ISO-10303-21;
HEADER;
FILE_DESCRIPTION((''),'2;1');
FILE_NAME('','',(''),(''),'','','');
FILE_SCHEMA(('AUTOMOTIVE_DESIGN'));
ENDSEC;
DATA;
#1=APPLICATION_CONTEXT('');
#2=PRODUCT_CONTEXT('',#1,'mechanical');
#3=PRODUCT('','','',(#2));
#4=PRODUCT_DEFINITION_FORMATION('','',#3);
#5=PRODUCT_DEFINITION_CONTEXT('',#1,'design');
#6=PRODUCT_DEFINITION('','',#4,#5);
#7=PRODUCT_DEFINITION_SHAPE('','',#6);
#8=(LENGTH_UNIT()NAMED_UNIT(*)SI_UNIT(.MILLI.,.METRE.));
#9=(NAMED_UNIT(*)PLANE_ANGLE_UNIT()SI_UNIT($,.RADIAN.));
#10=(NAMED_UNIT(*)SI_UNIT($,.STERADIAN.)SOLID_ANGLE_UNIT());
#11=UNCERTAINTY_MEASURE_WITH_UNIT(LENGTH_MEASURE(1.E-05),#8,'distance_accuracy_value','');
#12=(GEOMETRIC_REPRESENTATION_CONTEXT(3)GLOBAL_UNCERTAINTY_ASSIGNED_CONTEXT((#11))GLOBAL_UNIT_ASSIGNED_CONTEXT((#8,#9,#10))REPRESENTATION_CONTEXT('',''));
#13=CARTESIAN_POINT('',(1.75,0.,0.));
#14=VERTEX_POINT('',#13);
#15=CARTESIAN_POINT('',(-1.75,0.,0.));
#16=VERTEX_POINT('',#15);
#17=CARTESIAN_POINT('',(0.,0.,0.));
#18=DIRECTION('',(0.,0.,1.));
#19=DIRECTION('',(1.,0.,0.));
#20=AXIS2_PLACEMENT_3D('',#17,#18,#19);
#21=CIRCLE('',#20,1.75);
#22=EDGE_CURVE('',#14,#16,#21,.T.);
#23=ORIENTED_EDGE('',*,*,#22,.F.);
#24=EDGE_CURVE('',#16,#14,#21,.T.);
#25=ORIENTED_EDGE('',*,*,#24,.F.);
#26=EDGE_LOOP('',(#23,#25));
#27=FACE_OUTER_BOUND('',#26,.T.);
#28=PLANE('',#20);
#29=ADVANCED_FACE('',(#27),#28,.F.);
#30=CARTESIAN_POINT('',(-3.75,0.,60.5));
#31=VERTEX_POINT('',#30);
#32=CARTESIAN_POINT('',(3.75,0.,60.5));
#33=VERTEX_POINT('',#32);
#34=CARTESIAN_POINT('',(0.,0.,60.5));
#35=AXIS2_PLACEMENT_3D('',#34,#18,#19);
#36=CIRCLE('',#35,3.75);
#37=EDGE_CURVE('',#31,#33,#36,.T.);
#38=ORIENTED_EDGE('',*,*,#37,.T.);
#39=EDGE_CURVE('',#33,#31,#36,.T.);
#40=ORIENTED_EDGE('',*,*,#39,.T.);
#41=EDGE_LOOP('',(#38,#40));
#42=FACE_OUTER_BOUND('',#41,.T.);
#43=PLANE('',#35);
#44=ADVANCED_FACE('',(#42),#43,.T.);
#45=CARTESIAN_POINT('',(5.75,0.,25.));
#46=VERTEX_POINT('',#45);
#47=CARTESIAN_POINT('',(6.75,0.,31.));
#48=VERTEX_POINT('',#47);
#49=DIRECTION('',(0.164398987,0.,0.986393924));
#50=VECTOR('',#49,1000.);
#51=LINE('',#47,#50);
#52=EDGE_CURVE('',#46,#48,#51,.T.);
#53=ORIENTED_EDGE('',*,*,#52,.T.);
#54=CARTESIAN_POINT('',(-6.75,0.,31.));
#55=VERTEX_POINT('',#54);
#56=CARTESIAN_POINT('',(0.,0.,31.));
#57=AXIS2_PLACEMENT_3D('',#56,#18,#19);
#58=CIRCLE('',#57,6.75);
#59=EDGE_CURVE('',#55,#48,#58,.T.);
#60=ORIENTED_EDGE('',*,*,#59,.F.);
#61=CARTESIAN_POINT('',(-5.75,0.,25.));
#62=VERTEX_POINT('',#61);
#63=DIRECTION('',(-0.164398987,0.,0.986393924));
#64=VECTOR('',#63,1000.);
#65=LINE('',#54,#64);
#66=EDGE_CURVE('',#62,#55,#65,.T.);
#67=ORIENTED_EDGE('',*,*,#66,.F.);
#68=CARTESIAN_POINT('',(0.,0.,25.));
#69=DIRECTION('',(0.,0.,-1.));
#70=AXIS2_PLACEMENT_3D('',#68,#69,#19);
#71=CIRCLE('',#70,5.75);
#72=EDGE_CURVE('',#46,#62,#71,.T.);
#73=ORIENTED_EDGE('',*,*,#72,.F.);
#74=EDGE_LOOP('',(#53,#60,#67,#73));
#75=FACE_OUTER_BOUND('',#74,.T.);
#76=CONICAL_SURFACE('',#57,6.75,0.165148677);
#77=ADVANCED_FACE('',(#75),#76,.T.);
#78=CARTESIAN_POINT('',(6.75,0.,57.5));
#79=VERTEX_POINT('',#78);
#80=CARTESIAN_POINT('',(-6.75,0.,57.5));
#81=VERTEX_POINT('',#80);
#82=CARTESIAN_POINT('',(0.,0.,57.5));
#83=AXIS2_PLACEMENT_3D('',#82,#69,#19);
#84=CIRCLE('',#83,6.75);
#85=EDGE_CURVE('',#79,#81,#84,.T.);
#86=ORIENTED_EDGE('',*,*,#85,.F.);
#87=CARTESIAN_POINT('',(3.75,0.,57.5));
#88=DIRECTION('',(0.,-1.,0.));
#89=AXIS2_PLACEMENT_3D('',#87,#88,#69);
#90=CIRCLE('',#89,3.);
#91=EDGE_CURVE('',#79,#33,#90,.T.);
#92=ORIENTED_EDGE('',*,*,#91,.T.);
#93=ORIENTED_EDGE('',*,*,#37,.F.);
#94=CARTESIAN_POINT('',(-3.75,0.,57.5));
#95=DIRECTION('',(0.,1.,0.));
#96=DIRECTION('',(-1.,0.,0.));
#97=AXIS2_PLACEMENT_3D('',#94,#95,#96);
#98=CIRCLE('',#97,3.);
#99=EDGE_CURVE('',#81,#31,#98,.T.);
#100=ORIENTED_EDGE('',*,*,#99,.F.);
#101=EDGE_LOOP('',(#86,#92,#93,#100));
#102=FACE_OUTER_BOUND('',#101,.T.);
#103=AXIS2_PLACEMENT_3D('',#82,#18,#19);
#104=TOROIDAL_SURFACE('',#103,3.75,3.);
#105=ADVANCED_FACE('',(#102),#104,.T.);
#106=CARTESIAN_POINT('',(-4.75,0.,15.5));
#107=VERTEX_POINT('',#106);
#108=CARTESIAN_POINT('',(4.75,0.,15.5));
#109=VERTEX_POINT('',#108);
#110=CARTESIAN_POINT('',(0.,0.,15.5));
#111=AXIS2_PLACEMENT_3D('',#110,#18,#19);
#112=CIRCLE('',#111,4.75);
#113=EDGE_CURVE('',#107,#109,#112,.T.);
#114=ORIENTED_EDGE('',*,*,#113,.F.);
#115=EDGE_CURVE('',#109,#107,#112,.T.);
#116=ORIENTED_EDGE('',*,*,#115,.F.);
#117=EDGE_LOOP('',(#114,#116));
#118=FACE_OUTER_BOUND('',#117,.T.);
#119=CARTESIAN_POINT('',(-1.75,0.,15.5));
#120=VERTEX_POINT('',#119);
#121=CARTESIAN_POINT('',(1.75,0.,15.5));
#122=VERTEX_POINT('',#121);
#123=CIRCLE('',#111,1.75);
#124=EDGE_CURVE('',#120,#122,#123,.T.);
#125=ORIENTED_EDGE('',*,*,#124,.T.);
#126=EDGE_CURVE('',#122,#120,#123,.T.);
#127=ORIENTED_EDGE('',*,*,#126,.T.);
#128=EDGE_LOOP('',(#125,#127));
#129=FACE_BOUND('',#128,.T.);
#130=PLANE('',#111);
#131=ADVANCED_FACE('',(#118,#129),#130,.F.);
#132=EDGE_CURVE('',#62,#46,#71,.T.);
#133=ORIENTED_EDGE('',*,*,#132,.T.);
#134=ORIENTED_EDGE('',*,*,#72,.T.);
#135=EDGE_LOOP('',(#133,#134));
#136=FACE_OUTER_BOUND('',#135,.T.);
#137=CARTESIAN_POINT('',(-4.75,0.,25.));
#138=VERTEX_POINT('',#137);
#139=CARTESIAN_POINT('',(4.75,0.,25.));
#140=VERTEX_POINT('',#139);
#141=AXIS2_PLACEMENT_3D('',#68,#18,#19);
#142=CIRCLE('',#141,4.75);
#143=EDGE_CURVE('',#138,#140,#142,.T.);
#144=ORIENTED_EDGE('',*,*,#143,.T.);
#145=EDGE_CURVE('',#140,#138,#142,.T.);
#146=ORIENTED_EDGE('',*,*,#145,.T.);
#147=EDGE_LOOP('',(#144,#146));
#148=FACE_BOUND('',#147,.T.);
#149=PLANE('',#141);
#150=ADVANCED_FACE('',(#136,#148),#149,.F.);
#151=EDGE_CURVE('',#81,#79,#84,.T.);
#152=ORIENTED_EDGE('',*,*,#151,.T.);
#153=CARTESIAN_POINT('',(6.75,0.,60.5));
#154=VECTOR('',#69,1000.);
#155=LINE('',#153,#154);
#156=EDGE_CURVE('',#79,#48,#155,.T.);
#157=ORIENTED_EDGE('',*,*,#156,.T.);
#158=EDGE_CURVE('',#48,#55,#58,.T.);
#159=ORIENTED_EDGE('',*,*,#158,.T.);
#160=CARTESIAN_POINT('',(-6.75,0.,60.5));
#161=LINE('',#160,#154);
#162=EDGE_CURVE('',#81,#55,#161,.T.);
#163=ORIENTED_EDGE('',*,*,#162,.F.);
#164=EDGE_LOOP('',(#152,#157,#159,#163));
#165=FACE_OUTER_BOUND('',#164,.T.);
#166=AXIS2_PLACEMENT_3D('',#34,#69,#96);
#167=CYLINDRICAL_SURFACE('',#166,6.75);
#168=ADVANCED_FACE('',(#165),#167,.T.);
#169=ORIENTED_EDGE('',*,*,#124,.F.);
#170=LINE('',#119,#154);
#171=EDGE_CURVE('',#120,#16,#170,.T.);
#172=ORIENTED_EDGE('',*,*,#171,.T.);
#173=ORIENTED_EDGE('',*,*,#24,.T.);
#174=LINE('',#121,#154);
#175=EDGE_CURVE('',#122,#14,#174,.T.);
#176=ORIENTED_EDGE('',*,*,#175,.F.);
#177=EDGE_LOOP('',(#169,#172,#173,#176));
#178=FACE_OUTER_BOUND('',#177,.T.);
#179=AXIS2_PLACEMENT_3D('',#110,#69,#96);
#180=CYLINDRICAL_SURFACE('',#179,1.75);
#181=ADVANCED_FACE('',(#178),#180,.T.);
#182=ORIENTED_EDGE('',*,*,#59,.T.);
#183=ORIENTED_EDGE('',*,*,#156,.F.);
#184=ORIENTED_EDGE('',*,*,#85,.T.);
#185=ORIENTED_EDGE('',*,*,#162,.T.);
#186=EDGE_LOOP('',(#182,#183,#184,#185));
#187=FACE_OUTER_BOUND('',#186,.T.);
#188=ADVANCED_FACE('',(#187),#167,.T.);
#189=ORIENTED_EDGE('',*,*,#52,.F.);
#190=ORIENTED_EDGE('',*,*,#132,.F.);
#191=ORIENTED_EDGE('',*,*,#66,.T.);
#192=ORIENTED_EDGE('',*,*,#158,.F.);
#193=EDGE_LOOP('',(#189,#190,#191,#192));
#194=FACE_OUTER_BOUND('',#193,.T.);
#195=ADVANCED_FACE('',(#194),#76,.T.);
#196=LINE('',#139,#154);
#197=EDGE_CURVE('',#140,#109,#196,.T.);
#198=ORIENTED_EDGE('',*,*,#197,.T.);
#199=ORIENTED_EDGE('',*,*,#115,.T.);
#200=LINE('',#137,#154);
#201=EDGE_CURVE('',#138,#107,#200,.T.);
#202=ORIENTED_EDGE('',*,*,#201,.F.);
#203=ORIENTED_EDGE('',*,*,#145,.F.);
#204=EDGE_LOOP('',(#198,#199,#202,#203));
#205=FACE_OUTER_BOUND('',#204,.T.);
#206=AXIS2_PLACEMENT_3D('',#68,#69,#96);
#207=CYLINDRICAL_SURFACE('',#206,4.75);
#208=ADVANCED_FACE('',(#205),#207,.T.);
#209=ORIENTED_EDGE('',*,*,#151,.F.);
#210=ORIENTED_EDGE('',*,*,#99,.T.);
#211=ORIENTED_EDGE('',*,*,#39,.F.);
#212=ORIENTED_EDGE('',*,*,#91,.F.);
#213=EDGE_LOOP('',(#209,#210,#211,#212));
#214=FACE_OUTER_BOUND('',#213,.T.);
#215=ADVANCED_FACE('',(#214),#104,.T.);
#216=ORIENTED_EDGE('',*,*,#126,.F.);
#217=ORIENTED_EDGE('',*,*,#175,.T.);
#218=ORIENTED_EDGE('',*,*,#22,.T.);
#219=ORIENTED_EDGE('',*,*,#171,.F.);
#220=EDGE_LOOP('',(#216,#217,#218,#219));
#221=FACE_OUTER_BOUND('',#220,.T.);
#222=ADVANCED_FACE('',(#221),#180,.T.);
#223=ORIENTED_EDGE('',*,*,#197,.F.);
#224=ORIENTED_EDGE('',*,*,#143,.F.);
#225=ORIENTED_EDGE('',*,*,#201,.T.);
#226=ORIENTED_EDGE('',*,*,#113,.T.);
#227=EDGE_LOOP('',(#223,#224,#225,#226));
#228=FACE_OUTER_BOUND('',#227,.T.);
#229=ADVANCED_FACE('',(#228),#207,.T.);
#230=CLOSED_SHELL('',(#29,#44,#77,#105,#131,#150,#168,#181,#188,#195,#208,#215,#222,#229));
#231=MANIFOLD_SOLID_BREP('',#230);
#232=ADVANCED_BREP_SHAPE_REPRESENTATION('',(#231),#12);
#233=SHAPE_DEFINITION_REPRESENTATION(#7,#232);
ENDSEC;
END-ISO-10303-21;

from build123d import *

# Parameters (mm, degrees)
SKETCH1_R           = 1.75
BOSS_EXTRUDE1_DEPTH = 15.5
SKETCH2_R           = 4.75
BOSS_EXTRUDE2_DEPTH = 9.5
SKETCH3_R           = 6.75
BOSS_EXTRUDE3_DEPTH = 35.5
CHAMFER1_SIZE       = 1
CHAMFER1_SIZE2      = 6
FILLET1_R           = 3


with BuildPart() as part:
    # Sketch1 → Boss-Extrude1 (new body)
    with BuildSketch(Plane.XY):
        Circle(SKETCH1_R)
    extrude(amount=BOSS_EXTRUDE1_DEPTH)

    # Sketch2 → Boss-Extrude2 (add)
    with BuildSketch(Plane.XY.offset(15.5)):
        Circle(SKETCH2_R)
    extrude(amount=BOSS_EXTRUDE2_DEPTH)

    # Sketch3 → Boss-Extrude3 (add)
    with BuildSketch(Plane.XY.offset(25)):
        Circle(SKETCH3_R)
    extrude(amount=BOSS_EXTRUDE3_DEPTH)

    # Chamfer1
    chamfer1_edges = [part.edges().sort_by_distance(p)[0] for p in [
        (-6.75, 0, 25),
    ]]
    chamfer1_side = [part.faces().sort_by_distance(p)[0] for p in [
        (-6.559081169, 0, 25),
    ]]
    chamfer(chamfer1_edges, length=CHAMFER1_SIZE, length2=CHAMFER1_SIZE2, reference=chamfer1_side[0])

    # Fillet1
    fillet1_edges = [part.edges().sort_by_distance(p)[0] for p in [
        (-6.75, 0, 60.5),
    ]]
    fillet(fillet1_edges, radius=FILLET1_R)


solid = part.part
